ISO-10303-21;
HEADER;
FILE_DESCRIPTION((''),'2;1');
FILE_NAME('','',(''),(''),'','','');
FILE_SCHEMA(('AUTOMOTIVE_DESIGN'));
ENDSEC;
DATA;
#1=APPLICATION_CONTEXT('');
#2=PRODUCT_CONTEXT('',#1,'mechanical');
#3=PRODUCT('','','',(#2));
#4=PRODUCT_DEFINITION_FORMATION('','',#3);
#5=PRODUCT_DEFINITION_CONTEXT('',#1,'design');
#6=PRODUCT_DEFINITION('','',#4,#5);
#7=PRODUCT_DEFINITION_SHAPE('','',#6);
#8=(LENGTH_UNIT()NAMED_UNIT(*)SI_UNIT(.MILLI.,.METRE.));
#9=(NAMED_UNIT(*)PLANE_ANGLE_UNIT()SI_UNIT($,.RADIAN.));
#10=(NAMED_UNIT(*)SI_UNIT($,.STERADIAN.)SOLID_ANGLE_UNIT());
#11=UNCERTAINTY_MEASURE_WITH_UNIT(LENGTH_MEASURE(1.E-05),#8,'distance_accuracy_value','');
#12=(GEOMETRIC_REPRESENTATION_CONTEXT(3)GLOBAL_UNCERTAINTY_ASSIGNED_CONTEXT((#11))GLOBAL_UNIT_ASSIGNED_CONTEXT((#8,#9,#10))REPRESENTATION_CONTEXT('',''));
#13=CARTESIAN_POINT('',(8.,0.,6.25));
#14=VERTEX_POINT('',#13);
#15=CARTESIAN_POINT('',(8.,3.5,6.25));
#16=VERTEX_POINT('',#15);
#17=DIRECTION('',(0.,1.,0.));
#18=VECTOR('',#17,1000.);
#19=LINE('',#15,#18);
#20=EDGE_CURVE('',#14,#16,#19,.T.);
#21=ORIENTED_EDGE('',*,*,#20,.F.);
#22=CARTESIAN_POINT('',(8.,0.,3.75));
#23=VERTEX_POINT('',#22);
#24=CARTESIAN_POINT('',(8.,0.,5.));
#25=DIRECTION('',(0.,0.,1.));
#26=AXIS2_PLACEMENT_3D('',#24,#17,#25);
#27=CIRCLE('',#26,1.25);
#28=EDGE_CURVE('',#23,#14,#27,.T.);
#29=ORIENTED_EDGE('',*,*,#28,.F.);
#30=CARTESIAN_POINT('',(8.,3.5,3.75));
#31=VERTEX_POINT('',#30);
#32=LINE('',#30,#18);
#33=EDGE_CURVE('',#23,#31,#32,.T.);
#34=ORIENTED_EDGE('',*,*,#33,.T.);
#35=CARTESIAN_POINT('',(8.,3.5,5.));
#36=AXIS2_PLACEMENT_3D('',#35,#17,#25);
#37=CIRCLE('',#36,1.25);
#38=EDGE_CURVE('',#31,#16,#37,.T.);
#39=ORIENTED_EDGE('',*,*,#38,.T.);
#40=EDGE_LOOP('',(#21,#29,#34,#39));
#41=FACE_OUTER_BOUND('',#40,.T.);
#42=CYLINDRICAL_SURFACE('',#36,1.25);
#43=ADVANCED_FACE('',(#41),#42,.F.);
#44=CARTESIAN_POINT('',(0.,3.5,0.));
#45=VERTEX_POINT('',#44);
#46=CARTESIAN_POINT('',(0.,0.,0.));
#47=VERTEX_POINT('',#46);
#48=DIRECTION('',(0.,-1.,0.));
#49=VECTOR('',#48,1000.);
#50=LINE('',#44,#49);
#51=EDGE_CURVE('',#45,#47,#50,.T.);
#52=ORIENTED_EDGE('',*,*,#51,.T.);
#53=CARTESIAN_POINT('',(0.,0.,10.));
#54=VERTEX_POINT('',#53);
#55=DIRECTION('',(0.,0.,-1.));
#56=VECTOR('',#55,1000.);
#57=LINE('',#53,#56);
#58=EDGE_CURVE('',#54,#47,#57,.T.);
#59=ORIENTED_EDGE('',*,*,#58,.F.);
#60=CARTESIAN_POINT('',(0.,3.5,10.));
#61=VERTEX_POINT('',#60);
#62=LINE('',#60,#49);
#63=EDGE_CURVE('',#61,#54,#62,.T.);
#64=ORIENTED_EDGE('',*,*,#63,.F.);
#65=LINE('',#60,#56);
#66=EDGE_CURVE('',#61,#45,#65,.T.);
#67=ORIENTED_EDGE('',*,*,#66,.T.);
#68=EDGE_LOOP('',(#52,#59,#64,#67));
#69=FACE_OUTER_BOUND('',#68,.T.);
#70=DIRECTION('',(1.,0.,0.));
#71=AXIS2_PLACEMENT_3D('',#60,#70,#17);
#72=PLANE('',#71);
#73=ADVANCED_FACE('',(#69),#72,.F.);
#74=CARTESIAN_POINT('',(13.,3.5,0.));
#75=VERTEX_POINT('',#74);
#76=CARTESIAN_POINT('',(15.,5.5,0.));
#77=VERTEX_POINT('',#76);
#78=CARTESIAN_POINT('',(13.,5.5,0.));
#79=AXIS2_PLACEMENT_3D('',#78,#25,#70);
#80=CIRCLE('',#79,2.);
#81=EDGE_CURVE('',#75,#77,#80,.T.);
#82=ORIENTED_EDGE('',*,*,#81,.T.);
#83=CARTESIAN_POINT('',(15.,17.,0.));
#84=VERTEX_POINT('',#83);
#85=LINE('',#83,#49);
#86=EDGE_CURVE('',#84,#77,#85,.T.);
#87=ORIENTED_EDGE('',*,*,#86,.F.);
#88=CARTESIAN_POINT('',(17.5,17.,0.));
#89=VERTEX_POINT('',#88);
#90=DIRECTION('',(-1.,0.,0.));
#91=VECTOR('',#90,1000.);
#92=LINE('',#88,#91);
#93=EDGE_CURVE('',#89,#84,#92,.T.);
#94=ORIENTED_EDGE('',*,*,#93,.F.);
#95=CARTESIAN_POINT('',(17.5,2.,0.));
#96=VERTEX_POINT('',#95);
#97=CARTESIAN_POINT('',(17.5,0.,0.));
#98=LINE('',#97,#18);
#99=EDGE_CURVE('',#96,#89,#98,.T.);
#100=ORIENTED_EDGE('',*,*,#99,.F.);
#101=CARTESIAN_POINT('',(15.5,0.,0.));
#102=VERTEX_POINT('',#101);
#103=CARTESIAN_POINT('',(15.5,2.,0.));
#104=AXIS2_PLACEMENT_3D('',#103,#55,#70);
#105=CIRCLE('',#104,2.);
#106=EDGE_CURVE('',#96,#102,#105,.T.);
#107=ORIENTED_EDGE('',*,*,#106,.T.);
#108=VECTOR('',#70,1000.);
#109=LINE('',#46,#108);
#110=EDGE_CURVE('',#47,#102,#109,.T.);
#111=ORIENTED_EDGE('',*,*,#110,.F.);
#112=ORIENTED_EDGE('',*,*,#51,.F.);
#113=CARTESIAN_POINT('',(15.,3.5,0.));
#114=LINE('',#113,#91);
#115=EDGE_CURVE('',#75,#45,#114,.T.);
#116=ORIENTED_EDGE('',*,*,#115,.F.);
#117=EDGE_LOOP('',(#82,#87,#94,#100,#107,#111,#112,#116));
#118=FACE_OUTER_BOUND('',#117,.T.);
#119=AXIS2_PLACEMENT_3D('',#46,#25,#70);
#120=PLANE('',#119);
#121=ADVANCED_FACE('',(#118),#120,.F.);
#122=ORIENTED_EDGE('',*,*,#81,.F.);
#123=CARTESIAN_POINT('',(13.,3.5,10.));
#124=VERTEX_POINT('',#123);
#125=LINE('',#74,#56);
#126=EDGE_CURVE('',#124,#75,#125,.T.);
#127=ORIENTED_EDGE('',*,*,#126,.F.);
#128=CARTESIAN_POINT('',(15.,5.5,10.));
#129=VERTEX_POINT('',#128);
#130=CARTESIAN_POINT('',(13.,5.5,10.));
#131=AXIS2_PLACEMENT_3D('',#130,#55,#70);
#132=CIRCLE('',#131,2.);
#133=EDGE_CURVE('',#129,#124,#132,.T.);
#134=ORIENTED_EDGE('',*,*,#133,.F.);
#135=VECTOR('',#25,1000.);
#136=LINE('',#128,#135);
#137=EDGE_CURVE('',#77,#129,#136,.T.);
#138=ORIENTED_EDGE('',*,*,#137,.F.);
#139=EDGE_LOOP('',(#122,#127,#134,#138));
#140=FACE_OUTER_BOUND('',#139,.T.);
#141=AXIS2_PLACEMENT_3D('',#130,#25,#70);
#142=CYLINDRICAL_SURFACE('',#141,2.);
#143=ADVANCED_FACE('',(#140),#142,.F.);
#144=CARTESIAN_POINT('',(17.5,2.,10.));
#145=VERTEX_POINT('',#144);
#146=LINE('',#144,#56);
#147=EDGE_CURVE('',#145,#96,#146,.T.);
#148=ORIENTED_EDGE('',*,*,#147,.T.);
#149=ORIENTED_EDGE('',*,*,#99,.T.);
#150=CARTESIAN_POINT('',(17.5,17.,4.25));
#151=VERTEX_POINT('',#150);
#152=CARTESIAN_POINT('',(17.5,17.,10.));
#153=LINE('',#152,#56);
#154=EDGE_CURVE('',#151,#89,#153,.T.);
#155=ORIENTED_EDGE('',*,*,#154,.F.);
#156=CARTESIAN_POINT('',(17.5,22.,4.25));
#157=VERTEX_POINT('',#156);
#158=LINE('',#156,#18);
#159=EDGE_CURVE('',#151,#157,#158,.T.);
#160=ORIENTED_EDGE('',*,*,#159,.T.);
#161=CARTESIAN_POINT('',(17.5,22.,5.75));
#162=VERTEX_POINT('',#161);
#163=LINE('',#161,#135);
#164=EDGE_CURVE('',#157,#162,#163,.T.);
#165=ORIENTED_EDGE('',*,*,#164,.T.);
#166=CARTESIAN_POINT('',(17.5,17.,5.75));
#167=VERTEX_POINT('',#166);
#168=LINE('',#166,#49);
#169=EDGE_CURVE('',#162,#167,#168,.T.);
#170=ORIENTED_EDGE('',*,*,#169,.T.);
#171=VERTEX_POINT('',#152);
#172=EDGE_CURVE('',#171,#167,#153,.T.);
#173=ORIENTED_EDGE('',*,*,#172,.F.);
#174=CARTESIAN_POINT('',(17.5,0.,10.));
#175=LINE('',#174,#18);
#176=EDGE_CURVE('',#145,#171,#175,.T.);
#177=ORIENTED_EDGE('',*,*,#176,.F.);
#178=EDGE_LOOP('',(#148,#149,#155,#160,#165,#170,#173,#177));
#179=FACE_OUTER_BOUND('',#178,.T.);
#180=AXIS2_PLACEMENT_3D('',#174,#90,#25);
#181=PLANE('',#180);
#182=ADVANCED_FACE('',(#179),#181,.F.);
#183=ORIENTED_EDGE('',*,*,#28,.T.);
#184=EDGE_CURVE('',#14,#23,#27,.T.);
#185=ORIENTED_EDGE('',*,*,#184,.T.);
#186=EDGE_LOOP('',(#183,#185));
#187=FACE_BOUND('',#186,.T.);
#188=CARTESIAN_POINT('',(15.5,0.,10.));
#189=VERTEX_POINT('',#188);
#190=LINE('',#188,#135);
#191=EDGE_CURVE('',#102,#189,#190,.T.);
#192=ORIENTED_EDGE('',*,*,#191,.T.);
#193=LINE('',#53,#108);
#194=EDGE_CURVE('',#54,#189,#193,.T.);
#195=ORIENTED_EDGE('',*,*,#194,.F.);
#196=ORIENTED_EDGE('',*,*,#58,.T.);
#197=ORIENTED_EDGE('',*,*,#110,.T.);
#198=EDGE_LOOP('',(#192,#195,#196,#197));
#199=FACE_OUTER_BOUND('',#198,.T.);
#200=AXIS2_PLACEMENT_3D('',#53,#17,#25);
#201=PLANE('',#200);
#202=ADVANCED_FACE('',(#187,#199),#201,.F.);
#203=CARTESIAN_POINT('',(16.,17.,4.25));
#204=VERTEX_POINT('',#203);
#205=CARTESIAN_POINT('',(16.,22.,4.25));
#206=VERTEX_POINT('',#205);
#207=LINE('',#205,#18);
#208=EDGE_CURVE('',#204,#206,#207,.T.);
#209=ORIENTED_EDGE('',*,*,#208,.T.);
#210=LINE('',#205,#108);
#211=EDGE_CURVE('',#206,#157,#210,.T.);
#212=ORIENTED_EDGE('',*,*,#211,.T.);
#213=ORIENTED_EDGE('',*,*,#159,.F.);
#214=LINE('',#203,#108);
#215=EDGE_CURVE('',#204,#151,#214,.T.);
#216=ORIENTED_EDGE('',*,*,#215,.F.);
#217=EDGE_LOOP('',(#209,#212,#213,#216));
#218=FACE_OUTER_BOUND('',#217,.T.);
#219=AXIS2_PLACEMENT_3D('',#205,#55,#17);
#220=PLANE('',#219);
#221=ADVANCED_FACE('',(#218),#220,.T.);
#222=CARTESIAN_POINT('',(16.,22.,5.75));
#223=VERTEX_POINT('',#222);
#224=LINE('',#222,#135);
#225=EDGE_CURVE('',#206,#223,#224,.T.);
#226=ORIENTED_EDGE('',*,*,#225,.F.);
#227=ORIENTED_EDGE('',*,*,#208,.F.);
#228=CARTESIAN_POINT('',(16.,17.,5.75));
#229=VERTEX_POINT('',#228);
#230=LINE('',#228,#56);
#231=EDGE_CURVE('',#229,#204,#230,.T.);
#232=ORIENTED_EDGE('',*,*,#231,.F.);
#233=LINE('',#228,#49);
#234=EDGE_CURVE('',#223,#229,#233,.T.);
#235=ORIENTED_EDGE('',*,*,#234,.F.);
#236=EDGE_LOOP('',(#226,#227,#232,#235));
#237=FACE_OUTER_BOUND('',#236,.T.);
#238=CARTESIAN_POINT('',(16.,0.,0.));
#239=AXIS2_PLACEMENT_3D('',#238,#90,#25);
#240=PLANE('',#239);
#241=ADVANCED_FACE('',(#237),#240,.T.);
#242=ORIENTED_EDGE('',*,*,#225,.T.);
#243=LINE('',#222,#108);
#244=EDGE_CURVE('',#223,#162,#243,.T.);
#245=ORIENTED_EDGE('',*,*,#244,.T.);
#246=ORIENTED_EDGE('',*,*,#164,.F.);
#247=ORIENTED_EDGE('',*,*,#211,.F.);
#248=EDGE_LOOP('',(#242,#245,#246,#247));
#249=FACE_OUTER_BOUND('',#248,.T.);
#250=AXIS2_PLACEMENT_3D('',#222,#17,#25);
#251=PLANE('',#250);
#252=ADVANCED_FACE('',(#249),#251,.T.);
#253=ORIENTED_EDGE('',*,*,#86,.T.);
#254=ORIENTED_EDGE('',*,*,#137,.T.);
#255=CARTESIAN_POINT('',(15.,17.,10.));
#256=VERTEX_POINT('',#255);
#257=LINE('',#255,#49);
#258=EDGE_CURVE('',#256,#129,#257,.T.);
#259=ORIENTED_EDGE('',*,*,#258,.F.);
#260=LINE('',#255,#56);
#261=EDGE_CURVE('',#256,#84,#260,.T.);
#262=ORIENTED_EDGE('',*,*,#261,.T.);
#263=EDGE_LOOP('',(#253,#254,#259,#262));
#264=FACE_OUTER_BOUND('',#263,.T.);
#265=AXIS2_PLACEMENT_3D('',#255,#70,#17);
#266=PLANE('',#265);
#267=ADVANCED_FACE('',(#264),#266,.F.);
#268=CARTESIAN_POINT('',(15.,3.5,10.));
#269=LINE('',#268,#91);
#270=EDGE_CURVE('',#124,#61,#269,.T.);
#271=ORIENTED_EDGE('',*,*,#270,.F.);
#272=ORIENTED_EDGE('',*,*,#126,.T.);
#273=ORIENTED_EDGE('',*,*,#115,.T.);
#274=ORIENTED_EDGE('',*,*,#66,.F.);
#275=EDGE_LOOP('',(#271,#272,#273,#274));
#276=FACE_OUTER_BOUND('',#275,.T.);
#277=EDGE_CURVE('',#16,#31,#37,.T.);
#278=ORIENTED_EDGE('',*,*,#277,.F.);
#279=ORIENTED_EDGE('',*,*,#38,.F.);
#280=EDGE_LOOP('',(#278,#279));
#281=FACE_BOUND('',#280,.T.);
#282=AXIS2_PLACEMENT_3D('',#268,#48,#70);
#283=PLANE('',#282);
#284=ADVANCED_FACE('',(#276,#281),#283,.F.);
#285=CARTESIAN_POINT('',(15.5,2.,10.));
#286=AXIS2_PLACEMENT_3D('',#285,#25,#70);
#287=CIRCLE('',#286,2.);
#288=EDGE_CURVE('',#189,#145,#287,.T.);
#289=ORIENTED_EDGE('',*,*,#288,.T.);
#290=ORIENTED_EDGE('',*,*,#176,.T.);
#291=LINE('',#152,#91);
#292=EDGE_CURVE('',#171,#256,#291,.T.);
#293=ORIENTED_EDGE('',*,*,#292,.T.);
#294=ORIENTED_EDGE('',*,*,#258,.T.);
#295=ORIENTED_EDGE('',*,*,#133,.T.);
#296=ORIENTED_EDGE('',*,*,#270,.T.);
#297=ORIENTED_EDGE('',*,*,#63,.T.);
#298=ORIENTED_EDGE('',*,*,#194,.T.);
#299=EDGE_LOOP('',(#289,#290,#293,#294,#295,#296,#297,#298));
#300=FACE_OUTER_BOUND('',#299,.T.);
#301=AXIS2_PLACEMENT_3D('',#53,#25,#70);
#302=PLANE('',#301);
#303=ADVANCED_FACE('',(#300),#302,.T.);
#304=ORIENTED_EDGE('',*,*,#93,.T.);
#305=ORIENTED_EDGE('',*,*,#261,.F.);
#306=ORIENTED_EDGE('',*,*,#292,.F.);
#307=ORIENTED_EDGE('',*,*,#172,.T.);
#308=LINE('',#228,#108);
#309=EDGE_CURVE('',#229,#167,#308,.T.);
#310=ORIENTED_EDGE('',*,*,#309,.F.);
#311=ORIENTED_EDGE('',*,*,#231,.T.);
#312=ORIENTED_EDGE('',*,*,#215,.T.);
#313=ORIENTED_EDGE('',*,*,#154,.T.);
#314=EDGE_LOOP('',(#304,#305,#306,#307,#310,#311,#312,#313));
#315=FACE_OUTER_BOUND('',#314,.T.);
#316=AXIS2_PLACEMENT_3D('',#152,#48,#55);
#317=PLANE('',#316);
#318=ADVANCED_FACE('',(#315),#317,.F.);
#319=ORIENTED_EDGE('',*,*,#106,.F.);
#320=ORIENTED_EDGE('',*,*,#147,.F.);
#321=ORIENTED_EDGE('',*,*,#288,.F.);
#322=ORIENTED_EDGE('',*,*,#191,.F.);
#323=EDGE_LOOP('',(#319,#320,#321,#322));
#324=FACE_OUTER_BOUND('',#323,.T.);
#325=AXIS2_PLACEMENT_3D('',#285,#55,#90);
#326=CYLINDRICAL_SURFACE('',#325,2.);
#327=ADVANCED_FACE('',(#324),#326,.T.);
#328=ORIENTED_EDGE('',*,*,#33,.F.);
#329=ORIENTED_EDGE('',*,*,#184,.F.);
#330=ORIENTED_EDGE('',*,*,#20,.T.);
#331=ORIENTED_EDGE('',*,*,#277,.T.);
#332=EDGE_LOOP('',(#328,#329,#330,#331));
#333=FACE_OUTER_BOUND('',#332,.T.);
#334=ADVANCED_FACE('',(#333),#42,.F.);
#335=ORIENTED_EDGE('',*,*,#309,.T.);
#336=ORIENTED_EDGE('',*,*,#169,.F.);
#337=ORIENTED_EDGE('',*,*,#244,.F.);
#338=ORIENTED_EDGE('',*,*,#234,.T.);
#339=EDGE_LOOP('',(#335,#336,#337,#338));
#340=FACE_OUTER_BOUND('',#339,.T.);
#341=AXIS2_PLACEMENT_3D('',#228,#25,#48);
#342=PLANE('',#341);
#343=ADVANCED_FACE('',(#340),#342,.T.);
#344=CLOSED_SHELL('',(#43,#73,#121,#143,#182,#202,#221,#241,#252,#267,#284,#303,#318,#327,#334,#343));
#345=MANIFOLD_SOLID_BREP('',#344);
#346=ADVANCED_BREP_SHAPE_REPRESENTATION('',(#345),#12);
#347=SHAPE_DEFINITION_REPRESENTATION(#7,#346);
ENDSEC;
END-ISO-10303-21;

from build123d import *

# Parameters (mm, degrees)
BOSS_EXTRUDE1_DEPTH   = 10
SKETCH2_W             = 1.5
SKETCH2_H             = 5
BOSS_EXTRUDE2_DEPTH   = 1.5
FILLET1_R             = 2
M3_TAPPED_HOLE1_D     = 2.5
M3_TAPPED_HOLE1_DEPTH = 8.5
M3_TAPPED_HOLE1_TIP   = 0.751075774


with BuildPart() as part:
    # Sketch1 → Boss-Extrude1 (new body)
    with BuildSketch(Plane.XY):
        Polygon((0, 0), (17.5, 0), (17.5, 17), (15, 17), (15, 3.5), (0, 3.5), align=None)
    extrude(amount=BOSS_EXTRUDE1_DEPTH)

    # Sketch2 → Boss-Extrude2 (add)
    with BuildSketch(Plane(origin=(17.5, 0, 0), x_dir=(0, 0, -1), z_dir=(1, 0, 0))):
        with Locations((-5, 19.5)):
            Rectangle(SKETCH2_W, SKETCH2_H)
    extrude(amount=-BOSS_EXTRUDE2_DEPTH)

    # Fillet1
    fillet1_edges = [part.edges().sort_by_distance(p)[0] for p in [
        (15, 3.5, 5),
        (17.5, 0, 5),
    ]]
    fillet(fillet1_edges, radius=FILLET1_R)

    # M3 Tapped Hole1
    with Locations(Plane(origin=(0, 3.5, 0), x_dir=(1, 0, 0), z_dir=(0, 1, 0))):
        with Locations((8, -5)):
            Hole(M3_TAPPED_HOLE1_D / 2, depth=M3_TAPPED_HOLE1_DEPTH)
            with Locations((0, 0, -(M3_TAPPED_HOLE1_DEPTH + M3_TAPPED_HOLE1_TIP / 2))):  # 118° drill point
                Cone(0, M3_TAPPED_HOLE1_D / 2, M3_TAPPED_HOLE1_TIP, mode=Mode.SUBTRACT)


solid = part.part
